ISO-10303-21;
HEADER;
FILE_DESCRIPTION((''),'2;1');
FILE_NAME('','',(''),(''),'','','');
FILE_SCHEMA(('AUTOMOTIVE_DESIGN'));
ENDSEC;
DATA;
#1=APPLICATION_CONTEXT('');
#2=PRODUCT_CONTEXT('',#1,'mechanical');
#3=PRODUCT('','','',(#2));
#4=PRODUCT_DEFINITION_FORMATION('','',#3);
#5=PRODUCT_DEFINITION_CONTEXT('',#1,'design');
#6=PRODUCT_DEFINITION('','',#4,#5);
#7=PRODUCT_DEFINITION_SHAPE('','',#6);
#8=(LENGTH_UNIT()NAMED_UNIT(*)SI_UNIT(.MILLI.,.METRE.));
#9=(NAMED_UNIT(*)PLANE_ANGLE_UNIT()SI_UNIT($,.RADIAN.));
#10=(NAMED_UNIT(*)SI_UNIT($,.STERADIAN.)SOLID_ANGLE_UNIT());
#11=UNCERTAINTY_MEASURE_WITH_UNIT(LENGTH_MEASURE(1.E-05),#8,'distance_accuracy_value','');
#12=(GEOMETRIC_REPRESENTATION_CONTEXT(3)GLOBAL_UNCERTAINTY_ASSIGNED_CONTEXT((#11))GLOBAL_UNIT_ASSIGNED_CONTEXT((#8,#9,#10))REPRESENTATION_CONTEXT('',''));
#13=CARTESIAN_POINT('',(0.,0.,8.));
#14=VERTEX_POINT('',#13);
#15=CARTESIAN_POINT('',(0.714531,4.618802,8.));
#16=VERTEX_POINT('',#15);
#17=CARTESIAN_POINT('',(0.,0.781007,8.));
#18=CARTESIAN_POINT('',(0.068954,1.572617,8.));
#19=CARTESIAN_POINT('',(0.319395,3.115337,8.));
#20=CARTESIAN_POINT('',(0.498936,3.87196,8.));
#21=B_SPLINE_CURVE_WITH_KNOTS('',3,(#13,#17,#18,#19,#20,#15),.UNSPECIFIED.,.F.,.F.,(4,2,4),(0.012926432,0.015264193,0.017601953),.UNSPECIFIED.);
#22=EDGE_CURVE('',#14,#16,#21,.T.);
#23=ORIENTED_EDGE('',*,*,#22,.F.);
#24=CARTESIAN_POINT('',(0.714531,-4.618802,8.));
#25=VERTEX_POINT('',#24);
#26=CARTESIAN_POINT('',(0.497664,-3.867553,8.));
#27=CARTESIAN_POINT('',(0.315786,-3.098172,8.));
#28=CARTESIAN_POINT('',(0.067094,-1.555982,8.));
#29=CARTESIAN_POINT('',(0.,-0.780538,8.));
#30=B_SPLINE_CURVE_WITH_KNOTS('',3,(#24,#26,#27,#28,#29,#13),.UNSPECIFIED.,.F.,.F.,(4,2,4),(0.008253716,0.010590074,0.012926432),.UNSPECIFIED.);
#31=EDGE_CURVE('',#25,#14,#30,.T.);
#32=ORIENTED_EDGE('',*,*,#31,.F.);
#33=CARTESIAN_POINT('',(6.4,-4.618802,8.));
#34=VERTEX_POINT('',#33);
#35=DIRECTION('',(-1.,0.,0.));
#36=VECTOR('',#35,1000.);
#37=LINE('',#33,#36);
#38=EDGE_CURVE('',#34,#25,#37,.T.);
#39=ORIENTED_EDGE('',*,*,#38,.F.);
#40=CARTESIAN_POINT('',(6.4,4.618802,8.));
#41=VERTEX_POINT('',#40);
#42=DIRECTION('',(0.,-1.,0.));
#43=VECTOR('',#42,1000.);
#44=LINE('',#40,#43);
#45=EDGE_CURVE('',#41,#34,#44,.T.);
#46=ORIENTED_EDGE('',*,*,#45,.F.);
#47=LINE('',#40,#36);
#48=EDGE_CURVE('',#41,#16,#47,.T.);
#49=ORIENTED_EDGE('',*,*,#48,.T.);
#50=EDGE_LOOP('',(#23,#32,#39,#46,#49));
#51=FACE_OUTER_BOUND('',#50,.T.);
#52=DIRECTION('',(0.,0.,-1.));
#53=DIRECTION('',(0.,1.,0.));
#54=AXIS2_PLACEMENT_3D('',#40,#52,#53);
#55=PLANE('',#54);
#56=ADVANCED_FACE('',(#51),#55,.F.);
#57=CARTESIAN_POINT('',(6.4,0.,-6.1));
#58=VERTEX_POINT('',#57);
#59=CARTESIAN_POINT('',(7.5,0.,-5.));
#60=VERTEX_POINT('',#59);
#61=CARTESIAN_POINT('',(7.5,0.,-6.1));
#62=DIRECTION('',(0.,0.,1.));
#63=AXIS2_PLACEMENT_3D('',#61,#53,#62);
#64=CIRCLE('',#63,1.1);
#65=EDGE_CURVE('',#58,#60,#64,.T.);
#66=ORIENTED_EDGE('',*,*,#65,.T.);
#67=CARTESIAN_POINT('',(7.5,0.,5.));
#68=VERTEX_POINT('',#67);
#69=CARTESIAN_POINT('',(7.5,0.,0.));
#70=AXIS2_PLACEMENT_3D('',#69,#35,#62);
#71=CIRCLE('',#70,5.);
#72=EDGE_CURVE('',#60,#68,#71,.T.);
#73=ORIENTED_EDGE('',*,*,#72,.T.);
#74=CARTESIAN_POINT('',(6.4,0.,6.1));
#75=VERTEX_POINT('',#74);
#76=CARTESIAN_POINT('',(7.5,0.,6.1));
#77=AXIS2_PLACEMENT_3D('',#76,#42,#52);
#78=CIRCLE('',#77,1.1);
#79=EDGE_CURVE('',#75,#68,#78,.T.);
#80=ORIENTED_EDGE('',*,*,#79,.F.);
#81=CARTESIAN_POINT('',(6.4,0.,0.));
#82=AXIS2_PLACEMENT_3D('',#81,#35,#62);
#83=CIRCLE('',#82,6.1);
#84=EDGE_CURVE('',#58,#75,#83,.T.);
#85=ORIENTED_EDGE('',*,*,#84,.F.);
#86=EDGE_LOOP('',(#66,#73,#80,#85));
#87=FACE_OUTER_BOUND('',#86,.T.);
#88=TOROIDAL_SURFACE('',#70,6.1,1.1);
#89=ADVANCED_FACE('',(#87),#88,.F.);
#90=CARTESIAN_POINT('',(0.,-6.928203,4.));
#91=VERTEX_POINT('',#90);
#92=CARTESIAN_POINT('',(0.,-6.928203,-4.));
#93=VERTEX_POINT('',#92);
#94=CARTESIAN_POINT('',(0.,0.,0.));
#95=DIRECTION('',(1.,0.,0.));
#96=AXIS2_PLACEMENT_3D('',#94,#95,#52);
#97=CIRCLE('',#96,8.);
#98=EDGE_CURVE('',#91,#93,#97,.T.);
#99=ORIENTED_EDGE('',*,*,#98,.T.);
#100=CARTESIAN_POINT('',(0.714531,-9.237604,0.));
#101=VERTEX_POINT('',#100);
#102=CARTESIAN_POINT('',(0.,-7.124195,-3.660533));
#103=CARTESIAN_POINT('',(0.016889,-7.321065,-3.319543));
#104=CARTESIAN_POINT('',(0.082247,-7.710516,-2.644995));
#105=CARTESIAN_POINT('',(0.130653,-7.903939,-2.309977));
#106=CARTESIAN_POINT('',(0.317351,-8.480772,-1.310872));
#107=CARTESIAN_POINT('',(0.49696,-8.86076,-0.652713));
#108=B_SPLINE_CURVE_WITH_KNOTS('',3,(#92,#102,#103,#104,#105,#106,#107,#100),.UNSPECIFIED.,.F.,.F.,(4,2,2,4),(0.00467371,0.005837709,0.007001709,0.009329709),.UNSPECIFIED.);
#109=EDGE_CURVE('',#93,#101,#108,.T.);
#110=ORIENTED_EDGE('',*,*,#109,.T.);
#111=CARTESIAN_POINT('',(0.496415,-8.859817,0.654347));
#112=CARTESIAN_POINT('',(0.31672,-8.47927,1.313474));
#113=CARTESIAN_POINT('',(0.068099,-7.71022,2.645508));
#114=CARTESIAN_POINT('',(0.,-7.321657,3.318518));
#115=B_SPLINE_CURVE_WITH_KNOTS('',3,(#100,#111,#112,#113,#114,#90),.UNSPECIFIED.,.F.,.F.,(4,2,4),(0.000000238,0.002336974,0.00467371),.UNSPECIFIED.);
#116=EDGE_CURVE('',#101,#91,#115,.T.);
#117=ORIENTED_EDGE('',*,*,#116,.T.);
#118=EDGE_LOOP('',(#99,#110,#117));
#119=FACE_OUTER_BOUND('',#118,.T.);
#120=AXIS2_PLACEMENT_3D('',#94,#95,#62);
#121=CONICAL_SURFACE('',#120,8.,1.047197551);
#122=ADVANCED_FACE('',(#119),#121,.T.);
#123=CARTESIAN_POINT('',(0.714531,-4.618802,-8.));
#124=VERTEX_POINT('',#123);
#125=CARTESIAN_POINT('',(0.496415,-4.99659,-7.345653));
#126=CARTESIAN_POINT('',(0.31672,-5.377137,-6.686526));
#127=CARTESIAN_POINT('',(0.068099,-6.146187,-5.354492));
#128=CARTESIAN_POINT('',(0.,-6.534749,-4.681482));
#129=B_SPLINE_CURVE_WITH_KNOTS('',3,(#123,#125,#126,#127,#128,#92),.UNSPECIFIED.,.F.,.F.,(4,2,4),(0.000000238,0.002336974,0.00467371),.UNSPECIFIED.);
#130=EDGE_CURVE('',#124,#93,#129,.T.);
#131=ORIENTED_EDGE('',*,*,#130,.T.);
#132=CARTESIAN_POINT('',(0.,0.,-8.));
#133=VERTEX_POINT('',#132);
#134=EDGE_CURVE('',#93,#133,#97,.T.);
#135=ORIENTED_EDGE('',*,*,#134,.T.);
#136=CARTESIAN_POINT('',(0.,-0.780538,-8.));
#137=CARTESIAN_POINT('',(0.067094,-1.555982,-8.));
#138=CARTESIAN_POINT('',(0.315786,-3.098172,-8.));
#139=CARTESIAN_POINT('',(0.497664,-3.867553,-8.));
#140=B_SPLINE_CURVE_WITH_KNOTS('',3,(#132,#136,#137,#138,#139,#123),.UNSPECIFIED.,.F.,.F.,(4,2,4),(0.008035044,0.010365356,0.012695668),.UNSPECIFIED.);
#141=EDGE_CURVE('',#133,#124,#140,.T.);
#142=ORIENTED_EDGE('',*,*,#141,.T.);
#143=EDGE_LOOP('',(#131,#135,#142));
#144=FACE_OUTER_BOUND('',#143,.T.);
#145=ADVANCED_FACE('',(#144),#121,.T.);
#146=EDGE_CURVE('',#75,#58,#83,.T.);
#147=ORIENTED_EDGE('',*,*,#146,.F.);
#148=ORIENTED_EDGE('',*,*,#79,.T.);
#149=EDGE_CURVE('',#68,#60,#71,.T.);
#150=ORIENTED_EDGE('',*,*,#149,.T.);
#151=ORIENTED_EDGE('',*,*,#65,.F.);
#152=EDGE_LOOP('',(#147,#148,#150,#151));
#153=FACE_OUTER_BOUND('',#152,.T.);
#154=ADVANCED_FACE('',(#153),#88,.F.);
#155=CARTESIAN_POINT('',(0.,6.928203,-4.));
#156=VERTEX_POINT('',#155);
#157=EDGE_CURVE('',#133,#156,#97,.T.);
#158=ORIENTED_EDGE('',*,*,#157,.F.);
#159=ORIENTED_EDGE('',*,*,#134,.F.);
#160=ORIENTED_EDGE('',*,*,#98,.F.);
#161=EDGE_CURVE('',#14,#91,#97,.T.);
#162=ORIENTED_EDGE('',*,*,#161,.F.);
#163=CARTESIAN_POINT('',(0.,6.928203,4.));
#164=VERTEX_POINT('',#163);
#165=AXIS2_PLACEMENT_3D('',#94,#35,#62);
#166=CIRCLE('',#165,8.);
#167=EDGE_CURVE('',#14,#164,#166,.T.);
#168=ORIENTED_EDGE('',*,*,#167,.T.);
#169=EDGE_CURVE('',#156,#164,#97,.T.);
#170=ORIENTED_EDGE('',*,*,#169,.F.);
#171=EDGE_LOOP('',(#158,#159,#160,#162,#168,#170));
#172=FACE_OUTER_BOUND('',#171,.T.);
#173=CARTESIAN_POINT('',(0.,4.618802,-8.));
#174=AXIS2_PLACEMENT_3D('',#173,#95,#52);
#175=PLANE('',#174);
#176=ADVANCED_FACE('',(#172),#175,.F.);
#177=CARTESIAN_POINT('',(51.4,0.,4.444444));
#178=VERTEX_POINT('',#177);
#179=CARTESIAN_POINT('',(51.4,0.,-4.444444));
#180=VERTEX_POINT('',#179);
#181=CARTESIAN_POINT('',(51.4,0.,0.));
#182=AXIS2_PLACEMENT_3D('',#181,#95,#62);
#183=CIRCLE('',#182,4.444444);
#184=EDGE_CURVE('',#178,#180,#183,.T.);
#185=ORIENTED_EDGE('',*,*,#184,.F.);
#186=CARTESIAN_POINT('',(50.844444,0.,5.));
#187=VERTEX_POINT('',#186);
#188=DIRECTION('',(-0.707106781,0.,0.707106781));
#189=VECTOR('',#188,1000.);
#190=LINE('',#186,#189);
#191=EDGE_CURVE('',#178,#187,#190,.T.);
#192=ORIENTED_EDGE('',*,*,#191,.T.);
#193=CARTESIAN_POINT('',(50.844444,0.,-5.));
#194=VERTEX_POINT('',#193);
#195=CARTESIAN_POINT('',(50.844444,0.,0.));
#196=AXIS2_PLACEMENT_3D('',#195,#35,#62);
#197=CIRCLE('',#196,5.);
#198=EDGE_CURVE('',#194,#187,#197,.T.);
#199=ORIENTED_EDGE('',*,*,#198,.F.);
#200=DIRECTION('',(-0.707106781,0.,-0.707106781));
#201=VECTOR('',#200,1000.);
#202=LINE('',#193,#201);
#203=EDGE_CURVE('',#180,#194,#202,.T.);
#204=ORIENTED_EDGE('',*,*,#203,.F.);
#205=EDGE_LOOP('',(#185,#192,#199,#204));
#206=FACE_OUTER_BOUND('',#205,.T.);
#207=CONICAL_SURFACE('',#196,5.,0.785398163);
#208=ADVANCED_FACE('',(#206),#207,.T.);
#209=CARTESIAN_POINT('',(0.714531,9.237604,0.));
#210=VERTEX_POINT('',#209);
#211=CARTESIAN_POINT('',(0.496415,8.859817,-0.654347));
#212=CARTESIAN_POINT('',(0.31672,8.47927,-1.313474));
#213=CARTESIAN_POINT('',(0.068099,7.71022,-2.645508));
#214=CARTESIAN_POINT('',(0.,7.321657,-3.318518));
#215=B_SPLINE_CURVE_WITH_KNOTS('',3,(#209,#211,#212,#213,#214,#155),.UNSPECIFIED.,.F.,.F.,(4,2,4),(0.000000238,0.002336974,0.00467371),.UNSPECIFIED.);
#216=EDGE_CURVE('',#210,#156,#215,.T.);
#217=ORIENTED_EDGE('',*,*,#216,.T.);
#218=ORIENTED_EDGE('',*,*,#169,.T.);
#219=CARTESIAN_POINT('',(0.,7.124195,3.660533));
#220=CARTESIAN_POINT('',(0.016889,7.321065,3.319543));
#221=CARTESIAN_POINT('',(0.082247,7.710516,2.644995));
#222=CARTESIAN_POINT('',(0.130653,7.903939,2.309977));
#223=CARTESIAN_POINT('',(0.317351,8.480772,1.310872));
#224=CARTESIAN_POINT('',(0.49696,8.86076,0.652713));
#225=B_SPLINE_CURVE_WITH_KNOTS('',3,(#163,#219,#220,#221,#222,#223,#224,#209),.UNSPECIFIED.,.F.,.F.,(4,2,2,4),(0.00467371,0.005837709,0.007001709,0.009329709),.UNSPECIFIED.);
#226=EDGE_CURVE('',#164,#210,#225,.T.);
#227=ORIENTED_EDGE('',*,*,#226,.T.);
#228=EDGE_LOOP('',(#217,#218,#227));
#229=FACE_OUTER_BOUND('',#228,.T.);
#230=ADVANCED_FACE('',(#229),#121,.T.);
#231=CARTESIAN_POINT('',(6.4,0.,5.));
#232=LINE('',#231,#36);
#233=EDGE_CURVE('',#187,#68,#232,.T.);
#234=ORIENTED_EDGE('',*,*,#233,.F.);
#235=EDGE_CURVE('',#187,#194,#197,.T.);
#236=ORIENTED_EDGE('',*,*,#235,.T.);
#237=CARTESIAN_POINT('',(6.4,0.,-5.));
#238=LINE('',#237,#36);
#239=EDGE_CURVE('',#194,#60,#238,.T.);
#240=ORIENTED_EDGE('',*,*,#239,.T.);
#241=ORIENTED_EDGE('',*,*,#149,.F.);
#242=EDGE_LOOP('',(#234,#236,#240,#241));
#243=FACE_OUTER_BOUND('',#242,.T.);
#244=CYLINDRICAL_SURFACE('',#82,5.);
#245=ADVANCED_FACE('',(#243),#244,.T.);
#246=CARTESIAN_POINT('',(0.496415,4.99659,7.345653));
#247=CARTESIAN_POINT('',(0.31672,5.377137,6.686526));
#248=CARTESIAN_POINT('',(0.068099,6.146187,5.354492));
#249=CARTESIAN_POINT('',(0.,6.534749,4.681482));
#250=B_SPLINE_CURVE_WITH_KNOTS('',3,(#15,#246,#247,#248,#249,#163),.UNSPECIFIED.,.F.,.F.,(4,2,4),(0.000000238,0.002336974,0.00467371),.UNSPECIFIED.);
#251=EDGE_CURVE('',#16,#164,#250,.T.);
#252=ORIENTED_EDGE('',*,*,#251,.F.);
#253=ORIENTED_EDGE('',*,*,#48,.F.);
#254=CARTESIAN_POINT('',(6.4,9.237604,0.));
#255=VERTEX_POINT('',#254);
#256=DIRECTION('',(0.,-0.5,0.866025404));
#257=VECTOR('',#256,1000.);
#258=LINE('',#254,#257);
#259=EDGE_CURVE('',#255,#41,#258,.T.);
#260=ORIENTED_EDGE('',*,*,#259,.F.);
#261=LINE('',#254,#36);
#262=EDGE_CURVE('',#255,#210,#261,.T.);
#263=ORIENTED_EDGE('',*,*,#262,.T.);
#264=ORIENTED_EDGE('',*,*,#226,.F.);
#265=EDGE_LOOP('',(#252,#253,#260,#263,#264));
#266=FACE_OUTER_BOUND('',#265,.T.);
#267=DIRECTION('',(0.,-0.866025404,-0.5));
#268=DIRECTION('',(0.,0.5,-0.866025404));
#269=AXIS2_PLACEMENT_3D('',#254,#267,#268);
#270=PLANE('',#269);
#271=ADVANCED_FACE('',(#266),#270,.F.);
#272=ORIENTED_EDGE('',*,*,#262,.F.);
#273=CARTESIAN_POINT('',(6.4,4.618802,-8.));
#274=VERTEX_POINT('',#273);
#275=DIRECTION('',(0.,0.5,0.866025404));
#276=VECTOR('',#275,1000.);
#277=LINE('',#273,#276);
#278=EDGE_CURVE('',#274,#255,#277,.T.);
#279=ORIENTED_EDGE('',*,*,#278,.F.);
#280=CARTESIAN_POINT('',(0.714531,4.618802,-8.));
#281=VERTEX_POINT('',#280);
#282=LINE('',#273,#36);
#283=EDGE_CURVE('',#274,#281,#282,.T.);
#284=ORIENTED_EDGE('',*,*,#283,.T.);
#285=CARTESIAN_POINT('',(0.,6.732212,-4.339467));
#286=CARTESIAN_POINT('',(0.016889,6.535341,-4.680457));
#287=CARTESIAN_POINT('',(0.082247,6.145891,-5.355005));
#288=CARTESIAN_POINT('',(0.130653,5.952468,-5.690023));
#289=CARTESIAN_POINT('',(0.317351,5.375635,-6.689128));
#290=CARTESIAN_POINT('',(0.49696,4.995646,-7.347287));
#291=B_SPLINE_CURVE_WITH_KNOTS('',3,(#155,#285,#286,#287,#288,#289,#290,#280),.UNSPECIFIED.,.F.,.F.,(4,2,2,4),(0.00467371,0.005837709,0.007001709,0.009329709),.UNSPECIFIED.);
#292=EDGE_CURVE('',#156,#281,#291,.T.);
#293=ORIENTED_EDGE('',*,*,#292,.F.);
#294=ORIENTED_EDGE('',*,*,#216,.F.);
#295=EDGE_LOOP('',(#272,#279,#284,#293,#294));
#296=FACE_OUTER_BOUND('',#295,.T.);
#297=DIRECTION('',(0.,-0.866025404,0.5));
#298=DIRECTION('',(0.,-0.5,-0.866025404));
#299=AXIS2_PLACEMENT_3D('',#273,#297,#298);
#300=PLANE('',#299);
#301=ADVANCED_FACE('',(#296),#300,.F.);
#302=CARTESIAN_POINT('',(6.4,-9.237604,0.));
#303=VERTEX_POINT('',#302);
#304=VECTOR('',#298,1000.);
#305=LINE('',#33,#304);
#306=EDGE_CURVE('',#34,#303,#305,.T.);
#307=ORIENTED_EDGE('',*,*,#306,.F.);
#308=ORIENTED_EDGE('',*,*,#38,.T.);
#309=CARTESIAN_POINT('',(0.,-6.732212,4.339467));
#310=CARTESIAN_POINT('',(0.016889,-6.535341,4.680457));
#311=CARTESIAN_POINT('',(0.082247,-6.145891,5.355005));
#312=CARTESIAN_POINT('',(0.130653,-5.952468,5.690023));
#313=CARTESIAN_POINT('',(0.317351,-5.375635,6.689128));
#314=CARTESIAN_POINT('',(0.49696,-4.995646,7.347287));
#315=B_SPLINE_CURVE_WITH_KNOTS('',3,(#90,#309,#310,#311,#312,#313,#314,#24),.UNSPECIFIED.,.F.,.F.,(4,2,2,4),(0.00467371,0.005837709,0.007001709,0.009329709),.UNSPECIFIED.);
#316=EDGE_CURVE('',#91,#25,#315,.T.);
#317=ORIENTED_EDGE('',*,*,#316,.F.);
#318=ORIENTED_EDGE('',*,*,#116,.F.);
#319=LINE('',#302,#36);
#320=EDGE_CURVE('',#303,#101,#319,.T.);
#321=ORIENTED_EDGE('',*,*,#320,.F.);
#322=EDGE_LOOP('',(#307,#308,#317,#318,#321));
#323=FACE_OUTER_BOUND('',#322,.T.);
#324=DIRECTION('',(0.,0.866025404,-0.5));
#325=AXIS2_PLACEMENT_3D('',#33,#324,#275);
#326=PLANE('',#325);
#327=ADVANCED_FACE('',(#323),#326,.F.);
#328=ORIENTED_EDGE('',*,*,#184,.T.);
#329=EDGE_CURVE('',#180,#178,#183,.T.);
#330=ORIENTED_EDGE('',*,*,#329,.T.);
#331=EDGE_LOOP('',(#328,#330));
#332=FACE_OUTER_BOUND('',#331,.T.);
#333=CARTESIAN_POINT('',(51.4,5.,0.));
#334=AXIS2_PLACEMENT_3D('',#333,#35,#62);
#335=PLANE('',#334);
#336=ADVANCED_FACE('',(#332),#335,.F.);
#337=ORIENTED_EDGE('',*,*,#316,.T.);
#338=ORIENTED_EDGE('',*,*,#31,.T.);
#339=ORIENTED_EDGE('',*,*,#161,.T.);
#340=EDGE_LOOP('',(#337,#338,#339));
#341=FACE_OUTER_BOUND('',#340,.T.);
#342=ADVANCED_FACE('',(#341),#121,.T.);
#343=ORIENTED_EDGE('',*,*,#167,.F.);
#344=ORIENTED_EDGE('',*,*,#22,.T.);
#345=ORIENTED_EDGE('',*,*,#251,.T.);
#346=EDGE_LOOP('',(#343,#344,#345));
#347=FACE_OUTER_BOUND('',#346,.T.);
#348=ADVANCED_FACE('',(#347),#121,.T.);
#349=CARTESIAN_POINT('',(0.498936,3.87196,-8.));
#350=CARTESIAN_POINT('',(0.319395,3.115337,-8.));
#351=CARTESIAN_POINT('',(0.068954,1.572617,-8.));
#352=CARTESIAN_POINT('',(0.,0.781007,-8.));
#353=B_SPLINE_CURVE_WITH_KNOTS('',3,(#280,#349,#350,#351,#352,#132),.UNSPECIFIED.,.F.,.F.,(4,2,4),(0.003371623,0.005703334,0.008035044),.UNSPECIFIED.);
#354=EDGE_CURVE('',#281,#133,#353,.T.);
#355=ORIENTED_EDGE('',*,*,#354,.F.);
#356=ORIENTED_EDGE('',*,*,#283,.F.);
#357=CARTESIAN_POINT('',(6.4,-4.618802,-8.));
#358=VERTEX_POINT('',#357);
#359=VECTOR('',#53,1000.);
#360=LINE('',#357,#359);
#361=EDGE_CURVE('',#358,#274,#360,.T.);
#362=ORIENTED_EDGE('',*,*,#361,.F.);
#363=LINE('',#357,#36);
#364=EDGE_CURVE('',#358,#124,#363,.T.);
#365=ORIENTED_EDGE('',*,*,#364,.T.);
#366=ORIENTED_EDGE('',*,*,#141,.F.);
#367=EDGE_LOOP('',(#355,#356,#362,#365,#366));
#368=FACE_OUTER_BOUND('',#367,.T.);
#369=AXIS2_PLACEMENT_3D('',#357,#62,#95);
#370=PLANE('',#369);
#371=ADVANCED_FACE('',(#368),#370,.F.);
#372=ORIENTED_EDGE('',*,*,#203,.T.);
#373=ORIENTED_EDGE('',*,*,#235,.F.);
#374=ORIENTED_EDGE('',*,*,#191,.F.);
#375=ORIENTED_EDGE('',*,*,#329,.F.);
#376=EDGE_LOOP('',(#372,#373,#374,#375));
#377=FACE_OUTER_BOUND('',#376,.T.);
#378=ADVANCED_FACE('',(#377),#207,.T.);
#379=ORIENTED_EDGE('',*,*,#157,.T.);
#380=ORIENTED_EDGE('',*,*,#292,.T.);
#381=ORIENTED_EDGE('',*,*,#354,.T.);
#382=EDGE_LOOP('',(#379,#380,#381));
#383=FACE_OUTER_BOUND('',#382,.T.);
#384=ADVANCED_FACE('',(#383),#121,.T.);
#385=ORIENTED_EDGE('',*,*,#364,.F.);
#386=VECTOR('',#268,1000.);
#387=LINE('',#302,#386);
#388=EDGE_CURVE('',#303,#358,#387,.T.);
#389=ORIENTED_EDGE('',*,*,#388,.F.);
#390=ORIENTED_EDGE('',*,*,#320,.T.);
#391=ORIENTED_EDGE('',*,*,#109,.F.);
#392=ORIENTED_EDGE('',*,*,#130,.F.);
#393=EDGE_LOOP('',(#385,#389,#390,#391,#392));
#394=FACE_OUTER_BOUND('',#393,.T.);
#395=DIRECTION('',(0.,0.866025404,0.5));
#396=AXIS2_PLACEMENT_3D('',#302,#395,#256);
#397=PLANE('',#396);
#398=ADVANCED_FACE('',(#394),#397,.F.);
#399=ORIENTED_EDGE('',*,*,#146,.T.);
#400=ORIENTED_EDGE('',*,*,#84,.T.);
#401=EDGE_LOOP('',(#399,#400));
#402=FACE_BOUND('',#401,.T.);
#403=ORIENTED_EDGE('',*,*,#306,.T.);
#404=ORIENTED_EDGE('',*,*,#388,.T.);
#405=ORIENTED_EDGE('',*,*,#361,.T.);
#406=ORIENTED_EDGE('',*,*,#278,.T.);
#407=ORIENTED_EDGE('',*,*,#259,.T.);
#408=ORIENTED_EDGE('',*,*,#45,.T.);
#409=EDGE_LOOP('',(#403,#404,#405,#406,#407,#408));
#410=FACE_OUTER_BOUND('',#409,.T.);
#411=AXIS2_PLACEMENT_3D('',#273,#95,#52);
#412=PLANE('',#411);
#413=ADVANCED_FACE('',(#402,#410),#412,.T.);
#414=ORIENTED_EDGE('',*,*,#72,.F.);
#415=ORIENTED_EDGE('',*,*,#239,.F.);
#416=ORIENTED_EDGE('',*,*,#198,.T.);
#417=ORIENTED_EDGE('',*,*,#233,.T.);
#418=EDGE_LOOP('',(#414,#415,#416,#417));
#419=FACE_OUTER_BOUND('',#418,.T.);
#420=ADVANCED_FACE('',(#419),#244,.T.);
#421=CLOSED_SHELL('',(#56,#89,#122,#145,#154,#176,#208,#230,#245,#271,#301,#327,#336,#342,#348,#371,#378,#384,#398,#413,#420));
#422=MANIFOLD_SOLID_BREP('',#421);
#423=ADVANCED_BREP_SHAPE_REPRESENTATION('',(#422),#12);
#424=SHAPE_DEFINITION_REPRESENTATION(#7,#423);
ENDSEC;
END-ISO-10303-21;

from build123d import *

# Parameters (mm, degrees)
BOSS_EXTRUDE1_DEPTH = 6.4
SKETCH4_R           = 17.59
SKETCH4_R_2         = 8
CUT_EXTRUDE1_DEPTH  = 0.8
CUT_EXTRUDE1_DRAFT  = -60
CHAMFER2_SIZE       = 0.555555556


with BuildPart() as part:
    # Sketch3 → Boss-Extrude1 (new body)
    with BuildSketch(Plane(origin=(0, 0, 0), x_dir=(0, 0, -1), z_dir=(1, 0, 0))):
        Polygon((8, 4.618802154), (0, 9.237604307), (-8, 4.618802154), (-8, -4.618802154), (0, -9.237604307), (8, -4.618802154), align=None)
    extrude(amount=BOSS_EXTRUDE1_DEPTH)


with BuildPart() as cut_extrude1_tool:
    # Sketch4 → Cut-Extrude1 (with draft: the straight prism first)
    with BuildSketch(Plane.ZY):
        Circle(SKETCH4_R)
        Circle(SKETCH4_R_2, mode=Mode.SUBTRACT)
    extrude(amount=-CUT_EXTRUDE1_DEPTH)
    # Cut-Extrude1: the draft: its side faces are tilted about the plane it starts from
    cut_extrude1_sides = [cut_extrude1_tool.faces().sort_by_distance(p)[0] for p in [
        (0.4, 0, -17.59),
        (0.4, 0, -8),
    ]]
    draft(cut_extrude1_sides, Plane.ZY, CUT_EXTRUDE1_DRAFT)


with BuildPart() as part_1:
    add(part.part)

    # Cut-Extrude1: cut by cut_extrude1_tool
    add(cut_extrude1_tool.part, mode=Mode.SUBTRACT)

    # Sketch5 → Revolve1 (revolve)
    with BuildSketch(Plane.XY, mode=Mode.PRIVATE) as revolve1_sk:
        with BuildLine():
            Line((7.5, 5), (51.4, 5))
            Line((51.4, 5), (51.4, 0))
            Line((51.4, 0), (6.4, 0))
            Line((6.4, 0), (6.4, 6.1))
            ThreePointArc((6.4, 6.1), (6.722182541, 5.322182541), (7.5, 5))
        make_face()
    revolve(revolve1_sk.sketch.rotate(Axis((6.4, 0, 0), (1, 0, 0)), 90), axis=Axis((6.4, 0, 0), (1, 0, 0)))

    # Chamfer2
    chamfer2_edges = [part_1.edges().sort_by_distance(p)[0] for p in [
        (51.4, 0, -5),
    ]]
    chamfer(chamfer2_edges, length=CHAMFER2_SIZE)


solid = part_1.part
